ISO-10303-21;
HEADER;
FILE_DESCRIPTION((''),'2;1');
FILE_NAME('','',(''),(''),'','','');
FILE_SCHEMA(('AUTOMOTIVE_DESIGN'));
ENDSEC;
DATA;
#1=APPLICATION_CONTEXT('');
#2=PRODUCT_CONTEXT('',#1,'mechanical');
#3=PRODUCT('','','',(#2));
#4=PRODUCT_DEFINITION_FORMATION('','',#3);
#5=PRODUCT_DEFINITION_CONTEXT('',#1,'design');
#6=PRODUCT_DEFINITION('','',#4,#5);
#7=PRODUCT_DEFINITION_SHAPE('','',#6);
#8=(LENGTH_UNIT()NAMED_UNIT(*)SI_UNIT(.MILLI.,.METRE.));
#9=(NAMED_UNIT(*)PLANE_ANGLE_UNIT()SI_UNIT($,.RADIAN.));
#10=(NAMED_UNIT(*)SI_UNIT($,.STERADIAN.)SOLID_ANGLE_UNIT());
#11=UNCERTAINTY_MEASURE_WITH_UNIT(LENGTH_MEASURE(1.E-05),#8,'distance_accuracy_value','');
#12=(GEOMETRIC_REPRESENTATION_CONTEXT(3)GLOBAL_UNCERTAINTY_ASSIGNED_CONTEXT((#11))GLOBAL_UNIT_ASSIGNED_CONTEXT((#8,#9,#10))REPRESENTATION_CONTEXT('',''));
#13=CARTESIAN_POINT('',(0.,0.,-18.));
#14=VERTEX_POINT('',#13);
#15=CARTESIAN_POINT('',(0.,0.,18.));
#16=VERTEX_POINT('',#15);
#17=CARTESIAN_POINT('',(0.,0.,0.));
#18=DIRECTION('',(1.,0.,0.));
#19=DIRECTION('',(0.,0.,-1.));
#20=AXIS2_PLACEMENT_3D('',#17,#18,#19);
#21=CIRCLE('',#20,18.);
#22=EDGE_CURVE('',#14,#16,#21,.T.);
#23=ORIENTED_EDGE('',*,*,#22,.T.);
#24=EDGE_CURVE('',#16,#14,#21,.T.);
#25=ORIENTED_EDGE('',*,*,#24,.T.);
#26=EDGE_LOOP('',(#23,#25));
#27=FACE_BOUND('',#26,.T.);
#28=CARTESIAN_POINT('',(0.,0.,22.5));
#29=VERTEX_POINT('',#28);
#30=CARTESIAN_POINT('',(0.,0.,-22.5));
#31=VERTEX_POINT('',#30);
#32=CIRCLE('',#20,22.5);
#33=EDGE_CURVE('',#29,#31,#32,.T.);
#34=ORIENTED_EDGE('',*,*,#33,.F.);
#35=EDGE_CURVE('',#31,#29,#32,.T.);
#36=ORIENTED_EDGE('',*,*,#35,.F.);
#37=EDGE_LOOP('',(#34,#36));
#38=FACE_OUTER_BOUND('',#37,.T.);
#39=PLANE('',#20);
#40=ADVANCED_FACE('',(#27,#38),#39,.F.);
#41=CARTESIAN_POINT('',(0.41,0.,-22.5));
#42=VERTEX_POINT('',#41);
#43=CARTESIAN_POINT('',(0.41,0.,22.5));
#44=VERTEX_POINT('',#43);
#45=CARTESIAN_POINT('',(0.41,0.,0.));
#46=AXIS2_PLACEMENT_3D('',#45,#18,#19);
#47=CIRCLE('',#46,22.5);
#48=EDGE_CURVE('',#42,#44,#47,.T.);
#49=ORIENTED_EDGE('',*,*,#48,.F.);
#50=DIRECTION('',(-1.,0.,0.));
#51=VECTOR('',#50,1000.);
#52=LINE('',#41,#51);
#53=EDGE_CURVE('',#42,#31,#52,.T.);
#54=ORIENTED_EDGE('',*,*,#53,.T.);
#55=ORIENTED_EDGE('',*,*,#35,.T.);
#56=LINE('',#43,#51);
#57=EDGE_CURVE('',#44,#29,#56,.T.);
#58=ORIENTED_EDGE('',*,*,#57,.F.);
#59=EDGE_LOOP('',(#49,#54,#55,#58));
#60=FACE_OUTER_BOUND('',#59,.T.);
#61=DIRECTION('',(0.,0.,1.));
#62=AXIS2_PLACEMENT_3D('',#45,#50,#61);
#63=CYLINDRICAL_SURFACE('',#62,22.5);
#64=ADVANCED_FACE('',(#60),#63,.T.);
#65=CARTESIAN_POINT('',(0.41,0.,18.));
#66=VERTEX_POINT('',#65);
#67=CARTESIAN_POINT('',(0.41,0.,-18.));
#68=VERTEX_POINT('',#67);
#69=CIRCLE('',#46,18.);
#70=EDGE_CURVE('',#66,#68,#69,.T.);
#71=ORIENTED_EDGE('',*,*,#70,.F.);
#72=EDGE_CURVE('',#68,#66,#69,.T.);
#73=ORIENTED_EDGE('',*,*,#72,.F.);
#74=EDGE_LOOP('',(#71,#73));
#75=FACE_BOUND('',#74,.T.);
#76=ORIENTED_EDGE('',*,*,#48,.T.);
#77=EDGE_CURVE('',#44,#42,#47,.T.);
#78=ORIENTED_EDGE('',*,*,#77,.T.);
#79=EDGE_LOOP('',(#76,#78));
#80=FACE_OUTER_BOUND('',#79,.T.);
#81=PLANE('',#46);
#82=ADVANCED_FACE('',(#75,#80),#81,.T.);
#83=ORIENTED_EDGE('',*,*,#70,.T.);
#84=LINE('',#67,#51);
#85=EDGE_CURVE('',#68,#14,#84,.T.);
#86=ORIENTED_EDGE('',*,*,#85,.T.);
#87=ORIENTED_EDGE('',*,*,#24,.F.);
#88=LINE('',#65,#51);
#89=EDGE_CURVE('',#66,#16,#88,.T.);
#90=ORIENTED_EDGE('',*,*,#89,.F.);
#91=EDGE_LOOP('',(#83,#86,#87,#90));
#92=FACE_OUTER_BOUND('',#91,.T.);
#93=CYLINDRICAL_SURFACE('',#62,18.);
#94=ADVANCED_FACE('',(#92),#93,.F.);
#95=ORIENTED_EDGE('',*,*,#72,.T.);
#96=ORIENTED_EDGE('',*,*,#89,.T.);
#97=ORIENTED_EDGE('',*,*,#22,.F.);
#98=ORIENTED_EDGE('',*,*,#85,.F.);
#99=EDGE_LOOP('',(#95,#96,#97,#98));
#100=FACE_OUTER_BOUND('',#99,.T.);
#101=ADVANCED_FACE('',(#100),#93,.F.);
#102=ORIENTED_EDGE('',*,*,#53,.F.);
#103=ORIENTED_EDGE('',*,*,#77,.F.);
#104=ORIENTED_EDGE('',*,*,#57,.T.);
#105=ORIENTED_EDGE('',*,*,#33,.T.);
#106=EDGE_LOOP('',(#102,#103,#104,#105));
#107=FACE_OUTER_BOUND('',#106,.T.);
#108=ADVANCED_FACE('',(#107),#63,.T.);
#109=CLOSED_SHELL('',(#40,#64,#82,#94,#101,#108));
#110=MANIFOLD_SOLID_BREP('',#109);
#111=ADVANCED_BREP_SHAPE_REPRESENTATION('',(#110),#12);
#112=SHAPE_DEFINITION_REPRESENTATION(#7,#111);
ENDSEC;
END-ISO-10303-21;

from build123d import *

# Parameters (mm, degrees)
SKETCH_1_R      = 22.5
SKETCH_1_R_2    = 18
EXTRUDE_1_DEPTH = 0.41


with BuildPart() as part:
    # 草图1 → 凸台-拉伸1 (new body)
    with BuildSketch(Plane(origin=(0, 0, 0), x_dir=(0, 0, -1), z_dir=(1, 0, 0))):
        Circle(SKETCH_1_R)
        Circle(SKETCH_1_R_2, mode=Mode.SUBTRACT)
    extrude(amount=EXTRUDE_1_DEPTH)


solid = part.part
